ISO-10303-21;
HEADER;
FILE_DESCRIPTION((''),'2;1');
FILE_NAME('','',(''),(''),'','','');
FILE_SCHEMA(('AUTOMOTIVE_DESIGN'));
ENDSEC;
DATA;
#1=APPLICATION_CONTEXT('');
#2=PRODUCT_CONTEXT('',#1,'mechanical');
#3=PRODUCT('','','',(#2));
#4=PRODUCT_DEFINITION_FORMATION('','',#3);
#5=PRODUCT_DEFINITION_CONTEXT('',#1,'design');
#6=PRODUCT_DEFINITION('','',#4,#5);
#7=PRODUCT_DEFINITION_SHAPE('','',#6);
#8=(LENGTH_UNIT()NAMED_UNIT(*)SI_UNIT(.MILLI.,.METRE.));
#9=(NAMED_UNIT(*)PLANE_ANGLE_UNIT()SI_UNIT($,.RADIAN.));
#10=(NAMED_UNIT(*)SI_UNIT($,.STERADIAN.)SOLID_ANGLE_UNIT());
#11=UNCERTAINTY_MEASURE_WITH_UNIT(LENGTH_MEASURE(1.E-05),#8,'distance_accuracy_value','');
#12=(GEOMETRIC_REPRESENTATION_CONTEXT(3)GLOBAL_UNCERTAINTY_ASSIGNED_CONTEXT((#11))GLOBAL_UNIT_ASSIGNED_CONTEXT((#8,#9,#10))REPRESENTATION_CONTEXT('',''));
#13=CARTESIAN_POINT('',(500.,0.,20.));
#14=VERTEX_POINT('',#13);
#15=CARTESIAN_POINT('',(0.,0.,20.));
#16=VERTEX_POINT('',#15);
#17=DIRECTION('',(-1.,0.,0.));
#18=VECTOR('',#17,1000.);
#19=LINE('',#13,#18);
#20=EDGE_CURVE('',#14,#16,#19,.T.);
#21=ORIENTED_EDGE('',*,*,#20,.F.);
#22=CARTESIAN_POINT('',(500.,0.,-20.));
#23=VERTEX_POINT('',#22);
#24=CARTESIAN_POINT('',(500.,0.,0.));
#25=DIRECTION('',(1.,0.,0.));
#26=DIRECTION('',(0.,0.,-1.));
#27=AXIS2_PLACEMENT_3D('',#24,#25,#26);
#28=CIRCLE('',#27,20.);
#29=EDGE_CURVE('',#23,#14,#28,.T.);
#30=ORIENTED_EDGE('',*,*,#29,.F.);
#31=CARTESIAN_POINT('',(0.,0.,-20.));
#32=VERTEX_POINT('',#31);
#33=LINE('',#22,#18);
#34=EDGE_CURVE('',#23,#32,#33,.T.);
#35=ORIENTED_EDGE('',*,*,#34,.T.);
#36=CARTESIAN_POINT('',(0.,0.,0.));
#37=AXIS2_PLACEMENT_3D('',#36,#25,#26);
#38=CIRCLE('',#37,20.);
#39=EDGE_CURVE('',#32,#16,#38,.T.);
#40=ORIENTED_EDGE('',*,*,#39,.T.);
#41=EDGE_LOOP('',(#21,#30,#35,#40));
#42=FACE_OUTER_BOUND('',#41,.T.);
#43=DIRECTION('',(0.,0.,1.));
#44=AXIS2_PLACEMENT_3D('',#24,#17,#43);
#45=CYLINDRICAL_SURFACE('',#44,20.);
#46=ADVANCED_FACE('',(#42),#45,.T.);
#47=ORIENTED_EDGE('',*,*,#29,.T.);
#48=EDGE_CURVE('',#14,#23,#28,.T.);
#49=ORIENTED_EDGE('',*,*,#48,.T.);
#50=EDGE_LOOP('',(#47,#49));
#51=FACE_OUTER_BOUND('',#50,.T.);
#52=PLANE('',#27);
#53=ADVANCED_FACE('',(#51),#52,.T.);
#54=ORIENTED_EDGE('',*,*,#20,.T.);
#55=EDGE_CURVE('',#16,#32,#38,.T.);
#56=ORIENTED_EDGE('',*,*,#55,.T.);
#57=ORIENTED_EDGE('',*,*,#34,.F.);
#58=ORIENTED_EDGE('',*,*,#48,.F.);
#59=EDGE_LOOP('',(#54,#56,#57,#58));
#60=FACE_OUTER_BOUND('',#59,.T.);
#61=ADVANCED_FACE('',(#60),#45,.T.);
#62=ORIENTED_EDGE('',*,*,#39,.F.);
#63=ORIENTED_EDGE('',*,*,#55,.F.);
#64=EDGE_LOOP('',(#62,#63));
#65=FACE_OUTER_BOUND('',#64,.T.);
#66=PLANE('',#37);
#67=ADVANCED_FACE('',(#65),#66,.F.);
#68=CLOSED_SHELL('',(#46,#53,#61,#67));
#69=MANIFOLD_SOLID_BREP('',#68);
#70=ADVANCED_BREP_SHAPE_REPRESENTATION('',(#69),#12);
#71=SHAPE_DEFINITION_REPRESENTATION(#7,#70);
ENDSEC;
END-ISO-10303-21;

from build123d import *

# Parameters (mm, degrees)
SKETCH1_R    = 20
LENGTH_DEPTH = 500


with BuildPart() as part:
    # Sketch1 → Length (new body)
    with BuildSketch(Plane(origin=(0, 0, 0), x_dir=(0, 0, -1), z_dir=(1, 0, 0))):
        Circle(SKETCH1_R)
    extrude(amount=LENGTH_DEPTH)


solid = part.part
